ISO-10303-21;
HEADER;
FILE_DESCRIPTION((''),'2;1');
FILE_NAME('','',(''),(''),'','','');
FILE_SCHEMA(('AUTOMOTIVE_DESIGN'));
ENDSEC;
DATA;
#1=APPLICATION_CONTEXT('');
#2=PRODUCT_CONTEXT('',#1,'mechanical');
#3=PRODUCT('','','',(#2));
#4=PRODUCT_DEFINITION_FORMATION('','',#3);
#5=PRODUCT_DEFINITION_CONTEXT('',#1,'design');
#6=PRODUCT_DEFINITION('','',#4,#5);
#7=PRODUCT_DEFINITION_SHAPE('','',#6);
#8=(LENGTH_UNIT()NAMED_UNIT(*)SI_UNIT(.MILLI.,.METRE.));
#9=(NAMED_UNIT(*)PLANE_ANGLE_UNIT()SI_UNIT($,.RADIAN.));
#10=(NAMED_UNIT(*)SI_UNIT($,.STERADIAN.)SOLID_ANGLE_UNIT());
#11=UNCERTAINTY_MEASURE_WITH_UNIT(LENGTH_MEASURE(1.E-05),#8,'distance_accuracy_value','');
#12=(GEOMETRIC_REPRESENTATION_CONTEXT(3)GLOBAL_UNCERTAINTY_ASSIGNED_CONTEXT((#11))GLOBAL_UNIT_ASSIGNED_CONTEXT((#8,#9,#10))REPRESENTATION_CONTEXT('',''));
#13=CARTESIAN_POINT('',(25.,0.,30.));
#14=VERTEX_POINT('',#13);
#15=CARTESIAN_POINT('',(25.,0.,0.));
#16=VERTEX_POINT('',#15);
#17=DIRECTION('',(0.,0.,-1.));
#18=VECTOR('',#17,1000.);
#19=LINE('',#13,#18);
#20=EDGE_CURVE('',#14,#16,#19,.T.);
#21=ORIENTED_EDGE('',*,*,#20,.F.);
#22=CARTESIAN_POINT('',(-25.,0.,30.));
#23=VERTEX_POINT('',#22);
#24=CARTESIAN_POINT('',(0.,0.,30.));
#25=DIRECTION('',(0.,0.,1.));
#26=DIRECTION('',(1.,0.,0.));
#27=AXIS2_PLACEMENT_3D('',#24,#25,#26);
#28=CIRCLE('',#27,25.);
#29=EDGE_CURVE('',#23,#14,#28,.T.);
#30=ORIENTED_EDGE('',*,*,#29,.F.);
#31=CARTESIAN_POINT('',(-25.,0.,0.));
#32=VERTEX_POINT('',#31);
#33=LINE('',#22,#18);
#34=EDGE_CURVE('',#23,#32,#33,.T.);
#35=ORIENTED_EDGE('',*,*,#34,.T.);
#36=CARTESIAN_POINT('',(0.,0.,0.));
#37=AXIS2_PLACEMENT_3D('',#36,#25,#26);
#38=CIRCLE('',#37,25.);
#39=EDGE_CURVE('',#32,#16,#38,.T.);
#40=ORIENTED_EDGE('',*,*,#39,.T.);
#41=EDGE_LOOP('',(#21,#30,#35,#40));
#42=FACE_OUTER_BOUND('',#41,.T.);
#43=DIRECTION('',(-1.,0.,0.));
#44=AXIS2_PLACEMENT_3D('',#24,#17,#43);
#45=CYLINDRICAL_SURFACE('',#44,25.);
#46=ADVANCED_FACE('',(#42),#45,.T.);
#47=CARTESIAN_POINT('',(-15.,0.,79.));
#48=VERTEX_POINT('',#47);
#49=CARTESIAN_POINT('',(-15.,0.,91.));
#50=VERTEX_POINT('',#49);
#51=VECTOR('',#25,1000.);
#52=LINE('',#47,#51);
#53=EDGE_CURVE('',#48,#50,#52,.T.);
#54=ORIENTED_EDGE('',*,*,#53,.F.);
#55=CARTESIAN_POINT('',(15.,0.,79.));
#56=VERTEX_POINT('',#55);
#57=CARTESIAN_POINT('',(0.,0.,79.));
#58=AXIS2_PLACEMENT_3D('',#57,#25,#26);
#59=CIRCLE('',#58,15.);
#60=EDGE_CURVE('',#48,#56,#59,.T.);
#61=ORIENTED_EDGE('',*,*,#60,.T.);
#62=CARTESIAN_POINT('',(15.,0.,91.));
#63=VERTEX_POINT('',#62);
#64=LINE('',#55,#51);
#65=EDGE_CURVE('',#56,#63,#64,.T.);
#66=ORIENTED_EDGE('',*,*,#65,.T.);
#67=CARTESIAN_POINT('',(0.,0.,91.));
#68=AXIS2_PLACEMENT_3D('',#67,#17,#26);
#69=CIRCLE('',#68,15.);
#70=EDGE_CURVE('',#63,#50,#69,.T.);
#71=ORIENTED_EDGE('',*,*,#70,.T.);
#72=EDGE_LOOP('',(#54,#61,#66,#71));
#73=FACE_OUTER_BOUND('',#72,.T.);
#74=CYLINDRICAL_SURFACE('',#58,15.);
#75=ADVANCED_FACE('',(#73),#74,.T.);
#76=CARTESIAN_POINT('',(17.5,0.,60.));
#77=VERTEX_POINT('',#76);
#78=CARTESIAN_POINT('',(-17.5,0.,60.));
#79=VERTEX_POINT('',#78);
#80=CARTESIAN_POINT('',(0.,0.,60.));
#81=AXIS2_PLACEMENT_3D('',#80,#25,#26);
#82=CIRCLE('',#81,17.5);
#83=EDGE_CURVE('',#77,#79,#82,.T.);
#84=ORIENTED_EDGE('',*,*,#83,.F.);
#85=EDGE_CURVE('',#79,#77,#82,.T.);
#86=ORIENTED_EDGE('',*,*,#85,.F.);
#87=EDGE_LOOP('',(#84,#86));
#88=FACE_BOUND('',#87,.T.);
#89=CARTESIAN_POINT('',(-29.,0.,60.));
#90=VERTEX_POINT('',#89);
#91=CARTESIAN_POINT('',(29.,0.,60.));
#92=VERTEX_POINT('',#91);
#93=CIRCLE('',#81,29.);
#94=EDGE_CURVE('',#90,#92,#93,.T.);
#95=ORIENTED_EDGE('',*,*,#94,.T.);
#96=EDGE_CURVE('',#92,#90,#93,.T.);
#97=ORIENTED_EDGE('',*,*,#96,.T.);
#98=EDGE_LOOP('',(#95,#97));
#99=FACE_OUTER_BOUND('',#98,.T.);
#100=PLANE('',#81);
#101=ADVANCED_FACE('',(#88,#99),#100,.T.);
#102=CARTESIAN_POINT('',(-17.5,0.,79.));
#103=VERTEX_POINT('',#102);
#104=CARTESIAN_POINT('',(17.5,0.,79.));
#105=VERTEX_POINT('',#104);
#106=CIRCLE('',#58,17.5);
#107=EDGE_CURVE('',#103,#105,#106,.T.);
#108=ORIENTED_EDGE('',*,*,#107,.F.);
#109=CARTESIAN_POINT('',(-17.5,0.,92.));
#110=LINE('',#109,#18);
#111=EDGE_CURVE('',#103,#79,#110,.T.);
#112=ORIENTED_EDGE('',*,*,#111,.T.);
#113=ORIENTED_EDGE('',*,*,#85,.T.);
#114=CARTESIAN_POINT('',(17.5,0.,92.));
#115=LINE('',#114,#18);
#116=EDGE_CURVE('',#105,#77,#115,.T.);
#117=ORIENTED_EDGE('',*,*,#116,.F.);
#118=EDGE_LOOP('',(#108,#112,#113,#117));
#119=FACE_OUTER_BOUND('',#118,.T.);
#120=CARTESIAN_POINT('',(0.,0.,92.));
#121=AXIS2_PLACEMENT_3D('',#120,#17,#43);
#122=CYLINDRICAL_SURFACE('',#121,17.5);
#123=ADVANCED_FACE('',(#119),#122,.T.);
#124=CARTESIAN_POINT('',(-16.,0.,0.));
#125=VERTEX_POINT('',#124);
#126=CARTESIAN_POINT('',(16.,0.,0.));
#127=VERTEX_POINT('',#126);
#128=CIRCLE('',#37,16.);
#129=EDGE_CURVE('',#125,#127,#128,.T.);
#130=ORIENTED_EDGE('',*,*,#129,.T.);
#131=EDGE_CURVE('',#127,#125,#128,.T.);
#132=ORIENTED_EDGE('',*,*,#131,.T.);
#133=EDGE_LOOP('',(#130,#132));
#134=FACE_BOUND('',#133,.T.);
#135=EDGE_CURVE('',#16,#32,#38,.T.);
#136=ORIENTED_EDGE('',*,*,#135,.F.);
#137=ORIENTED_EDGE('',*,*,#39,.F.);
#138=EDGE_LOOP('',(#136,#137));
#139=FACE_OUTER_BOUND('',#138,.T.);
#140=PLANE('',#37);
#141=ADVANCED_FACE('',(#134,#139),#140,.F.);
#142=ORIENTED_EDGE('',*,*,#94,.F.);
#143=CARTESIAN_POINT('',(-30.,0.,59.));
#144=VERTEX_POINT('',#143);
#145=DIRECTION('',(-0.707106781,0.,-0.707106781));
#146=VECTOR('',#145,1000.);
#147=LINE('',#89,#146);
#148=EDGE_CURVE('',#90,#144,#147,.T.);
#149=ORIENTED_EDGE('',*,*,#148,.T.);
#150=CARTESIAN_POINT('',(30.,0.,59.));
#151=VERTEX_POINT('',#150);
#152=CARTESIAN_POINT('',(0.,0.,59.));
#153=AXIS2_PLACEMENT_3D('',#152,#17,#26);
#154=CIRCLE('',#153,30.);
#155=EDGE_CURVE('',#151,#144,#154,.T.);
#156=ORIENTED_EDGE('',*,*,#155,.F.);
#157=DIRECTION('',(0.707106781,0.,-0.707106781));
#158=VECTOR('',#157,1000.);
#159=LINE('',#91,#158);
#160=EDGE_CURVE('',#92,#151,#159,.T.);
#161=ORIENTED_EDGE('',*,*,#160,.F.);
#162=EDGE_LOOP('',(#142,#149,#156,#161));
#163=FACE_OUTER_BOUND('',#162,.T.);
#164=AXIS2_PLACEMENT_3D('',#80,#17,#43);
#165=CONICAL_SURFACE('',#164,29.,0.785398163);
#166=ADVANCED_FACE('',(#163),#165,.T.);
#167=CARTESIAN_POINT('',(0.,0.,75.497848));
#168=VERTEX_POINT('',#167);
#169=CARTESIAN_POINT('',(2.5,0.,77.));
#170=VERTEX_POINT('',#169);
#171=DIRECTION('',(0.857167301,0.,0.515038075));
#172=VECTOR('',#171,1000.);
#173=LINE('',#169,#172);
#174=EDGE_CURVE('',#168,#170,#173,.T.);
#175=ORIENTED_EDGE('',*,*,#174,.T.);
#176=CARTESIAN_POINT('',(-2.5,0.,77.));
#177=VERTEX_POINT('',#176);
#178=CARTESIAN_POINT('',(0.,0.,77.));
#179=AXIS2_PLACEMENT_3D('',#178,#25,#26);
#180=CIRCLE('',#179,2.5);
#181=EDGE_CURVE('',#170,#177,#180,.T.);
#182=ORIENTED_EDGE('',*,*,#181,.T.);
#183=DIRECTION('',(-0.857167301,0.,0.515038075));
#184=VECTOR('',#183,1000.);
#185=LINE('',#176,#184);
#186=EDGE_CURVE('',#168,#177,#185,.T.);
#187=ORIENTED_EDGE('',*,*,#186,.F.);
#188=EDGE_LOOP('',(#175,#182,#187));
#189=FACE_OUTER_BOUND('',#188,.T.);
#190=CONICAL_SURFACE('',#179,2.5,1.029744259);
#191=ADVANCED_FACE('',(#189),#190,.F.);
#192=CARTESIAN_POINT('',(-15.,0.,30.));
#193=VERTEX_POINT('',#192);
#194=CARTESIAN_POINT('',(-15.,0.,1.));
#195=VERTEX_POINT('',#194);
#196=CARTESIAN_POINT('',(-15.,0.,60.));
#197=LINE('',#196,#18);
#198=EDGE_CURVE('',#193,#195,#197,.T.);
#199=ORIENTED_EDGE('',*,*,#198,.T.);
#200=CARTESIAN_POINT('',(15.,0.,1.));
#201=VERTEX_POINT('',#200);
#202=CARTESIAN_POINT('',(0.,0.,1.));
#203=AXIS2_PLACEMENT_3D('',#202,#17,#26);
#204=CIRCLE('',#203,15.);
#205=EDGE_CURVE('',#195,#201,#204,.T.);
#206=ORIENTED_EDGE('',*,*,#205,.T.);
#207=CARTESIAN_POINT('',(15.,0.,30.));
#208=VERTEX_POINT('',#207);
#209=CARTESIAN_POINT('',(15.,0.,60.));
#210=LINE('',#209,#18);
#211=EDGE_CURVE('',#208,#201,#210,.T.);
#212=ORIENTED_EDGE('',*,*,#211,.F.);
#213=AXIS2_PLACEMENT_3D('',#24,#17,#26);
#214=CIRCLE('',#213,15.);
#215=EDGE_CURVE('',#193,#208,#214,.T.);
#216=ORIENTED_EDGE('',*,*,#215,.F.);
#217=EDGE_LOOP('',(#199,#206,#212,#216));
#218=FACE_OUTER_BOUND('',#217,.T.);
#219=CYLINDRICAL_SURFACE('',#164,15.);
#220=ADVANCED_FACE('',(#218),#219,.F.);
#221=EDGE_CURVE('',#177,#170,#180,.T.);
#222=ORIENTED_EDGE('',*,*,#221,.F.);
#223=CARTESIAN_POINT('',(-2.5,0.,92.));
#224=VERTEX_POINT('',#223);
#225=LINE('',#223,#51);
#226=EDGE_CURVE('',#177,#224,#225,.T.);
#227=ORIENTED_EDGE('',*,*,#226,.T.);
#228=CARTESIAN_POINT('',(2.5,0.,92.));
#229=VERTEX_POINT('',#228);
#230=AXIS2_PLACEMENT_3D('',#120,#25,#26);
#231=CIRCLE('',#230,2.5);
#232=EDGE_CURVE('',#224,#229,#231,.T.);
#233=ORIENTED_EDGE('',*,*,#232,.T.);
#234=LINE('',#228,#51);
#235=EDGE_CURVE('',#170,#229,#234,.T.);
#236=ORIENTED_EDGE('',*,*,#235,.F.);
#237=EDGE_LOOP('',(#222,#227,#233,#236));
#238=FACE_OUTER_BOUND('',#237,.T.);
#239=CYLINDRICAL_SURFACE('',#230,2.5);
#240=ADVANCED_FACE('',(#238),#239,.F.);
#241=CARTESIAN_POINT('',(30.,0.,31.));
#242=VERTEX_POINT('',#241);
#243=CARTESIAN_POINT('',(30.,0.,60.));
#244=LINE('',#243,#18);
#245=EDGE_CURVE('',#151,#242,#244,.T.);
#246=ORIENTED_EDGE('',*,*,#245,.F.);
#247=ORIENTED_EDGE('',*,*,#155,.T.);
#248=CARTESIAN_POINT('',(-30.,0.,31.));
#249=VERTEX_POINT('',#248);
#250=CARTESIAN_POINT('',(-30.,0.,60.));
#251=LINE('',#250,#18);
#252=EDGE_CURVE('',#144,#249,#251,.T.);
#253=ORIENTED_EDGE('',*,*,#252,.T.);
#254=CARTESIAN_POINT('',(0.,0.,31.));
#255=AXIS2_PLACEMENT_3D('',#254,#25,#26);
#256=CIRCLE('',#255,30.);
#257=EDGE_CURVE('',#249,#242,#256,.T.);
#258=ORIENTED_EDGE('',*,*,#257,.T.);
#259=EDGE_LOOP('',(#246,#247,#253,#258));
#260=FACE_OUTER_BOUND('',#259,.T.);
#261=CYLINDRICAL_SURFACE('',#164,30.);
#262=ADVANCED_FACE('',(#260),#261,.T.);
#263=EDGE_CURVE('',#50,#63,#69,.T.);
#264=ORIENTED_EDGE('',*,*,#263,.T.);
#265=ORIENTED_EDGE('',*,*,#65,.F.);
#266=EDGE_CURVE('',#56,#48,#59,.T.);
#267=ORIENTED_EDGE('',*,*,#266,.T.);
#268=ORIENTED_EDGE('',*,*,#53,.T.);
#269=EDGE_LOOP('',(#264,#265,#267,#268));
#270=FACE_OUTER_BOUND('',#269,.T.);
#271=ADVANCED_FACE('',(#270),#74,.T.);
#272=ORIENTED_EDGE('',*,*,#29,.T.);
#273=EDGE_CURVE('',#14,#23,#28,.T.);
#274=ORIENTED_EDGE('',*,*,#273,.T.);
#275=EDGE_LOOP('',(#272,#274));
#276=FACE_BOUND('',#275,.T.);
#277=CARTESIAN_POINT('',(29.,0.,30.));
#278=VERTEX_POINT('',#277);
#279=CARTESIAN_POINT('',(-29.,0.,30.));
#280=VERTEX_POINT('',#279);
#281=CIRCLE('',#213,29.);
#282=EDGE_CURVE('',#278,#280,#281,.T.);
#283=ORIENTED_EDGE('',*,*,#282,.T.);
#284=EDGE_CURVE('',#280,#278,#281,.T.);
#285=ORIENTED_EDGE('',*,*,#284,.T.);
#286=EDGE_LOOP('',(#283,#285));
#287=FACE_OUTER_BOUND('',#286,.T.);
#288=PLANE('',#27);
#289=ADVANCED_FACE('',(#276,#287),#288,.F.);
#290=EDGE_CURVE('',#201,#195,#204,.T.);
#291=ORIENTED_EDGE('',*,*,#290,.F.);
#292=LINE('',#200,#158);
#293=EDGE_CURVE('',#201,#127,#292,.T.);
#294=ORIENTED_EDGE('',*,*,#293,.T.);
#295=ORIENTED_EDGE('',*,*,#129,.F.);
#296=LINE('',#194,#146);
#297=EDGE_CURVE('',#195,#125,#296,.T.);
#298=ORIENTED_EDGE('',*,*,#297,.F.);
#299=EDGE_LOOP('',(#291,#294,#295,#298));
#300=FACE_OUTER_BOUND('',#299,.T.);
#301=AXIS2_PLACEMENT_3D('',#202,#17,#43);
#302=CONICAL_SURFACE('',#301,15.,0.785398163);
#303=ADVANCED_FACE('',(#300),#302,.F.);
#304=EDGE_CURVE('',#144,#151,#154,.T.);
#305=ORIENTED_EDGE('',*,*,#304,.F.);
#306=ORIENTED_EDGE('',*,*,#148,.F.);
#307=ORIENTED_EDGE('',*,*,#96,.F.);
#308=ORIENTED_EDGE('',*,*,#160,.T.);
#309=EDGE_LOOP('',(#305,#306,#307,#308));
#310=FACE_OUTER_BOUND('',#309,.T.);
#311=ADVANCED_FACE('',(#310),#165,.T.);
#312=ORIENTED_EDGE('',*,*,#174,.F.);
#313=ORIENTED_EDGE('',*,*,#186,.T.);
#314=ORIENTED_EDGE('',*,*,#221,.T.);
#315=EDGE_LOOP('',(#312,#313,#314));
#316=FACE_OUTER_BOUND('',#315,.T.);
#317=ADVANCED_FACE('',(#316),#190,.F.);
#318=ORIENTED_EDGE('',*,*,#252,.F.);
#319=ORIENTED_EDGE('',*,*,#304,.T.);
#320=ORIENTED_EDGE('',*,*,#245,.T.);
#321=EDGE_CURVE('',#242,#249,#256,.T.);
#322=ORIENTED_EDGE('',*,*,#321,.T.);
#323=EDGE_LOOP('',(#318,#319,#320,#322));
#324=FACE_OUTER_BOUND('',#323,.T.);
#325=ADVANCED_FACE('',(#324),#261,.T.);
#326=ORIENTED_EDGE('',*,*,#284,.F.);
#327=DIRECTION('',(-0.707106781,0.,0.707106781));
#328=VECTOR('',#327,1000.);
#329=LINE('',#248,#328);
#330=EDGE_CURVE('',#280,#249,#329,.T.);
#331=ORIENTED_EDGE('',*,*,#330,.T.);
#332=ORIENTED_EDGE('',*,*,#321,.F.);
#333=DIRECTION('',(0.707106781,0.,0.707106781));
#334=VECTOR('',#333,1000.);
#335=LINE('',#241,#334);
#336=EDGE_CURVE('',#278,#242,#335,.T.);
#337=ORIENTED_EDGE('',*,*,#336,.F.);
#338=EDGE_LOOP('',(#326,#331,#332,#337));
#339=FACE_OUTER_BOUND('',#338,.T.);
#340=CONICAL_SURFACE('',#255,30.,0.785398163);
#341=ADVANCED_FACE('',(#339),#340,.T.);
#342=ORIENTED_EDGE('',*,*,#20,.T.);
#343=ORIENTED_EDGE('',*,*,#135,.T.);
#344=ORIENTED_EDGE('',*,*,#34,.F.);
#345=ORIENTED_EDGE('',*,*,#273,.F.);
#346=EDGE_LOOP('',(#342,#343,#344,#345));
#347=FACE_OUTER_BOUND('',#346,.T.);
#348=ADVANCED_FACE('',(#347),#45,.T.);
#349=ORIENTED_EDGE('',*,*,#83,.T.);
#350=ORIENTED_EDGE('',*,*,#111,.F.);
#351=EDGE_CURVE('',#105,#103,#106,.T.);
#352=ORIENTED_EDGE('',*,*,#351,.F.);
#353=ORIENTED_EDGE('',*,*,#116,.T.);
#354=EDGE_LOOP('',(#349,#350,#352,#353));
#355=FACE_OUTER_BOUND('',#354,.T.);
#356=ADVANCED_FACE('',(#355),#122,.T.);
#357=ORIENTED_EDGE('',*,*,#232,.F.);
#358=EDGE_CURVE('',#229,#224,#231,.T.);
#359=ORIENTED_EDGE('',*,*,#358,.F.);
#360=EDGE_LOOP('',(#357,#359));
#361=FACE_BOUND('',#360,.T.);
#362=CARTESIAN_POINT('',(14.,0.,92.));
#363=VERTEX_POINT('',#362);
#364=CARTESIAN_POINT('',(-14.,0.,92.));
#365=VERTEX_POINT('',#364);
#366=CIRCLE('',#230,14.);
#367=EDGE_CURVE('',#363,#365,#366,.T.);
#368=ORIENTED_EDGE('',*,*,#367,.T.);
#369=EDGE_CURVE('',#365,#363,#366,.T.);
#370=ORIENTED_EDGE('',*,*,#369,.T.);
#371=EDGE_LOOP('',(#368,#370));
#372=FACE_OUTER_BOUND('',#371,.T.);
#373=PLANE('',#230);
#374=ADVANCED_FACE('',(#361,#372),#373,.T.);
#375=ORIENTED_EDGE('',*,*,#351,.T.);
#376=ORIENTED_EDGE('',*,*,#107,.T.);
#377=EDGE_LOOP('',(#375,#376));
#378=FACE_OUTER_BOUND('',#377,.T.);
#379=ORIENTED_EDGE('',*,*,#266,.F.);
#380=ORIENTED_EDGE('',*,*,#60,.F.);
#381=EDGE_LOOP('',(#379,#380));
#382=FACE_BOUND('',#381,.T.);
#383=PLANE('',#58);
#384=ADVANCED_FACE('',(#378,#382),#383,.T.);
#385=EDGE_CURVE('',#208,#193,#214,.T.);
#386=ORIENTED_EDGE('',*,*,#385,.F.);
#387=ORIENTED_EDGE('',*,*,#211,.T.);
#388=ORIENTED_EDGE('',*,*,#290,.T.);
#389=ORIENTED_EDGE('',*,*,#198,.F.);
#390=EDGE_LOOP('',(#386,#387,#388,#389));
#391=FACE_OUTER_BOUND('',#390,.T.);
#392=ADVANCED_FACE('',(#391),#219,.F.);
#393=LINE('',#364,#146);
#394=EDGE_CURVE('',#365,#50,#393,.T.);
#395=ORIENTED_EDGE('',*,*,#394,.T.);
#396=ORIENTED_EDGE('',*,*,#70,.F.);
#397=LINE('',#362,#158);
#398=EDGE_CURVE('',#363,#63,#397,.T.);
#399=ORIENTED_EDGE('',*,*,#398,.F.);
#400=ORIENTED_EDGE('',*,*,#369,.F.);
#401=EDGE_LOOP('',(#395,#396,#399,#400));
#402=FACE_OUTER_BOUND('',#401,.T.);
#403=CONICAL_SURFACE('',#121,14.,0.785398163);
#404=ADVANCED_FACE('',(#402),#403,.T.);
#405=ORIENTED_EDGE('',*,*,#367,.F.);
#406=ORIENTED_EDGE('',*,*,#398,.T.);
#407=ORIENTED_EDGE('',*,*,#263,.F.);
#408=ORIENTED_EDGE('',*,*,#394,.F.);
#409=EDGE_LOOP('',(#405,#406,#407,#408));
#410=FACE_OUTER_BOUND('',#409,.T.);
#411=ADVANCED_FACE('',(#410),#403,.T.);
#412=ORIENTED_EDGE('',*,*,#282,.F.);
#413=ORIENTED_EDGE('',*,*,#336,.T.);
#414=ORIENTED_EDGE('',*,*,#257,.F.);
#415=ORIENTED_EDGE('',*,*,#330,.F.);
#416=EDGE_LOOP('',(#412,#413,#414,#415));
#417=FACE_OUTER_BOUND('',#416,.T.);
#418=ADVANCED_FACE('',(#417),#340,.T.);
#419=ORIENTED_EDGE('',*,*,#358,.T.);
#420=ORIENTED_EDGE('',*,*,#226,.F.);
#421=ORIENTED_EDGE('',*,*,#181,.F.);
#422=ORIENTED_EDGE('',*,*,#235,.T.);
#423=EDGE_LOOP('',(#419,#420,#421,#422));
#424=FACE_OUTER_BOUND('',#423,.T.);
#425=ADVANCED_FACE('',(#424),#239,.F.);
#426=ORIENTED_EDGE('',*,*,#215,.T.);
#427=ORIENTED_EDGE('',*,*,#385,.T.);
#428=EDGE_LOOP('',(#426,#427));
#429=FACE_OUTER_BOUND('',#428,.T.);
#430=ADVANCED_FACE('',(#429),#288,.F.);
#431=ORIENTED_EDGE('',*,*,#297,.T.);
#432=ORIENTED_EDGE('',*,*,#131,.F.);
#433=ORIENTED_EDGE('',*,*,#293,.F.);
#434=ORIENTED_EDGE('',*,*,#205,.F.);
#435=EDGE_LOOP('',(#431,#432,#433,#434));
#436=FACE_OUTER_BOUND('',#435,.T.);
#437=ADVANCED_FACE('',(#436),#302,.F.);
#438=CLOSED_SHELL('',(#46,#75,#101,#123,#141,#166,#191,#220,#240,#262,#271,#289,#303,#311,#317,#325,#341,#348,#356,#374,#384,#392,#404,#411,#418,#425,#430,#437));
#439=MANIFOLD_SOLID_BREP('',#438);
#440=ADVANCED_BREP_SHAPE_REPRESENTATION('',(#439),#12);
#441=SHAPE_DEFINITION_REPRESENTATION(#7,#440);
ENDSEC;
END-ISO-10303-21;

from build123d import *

# Parameters (mm, degrees)
SKETCH_1_R             = 25
EXTRUDE_1_DEPTH        = 30
SKETCH_2_R             = 30
EXTRUDE_2_DEPTH        = 30
SKETCH_4_R             = 15
CUT_EXTRUDE_1_DEPTH    = 74.484692283
EXTRUDE_START          = -30
SKETCH_13_R            = 15
EXTRUDE_4_DEPTH        = 30
SKETCH_12_R            = 17.5
EXTRUDE_3_DEPTH        = 32
HOLE_WIZARD_M6_1_D     = 5
HOLE_WIZARD_M6_1_DEPTH = 15
HOLE_WIZARD_M6_1_TIP   = 1.502151548
CUT_EXTRUDE_START      = -13
SKETCH_16_R            = 17.5
SKETCH_16_R_2          = 15
CUT_EXTRUDE_3_DEPTH    = 13
CHAMFER_4_SIZE         = 1


with BuildPart() as part:
    # 草图1 → 凸台-拉伸1 (new body)
    with BuildSketch(Plane.XY):
        Circle(SKETCH_1_R)
    extrude(amount=EXTRUDE_1_DEPTH)

    # 草图2 → 凸台-拉伸2 (add)
    with BuildSketch(Plane.XY.offset(30)):
        Circle(SKETCH_2_R)
    extrude(amount=EXTRUDE_2_DEPTH)

    # 草图4 → 切除-拉伸1 (cut, through all)
    with BuildSketch(Plane(origin=(0, 0, 0), x_dir=(-1, 0, 0), z_dir=(0, 0, -1))):
        Circle(SKETCH_4_R)
    extrude(amount=-CUT_EXTRUDE_1_DEPTH, mode=Mode.SUBTRACT)

    # 草图13 → 凸台-拉伸4 (add)
    with BuildSketch(Plane.XY.offset(60).offset(EXTRUDE_START)):
        with Locations(Location((0, 0, 0), (0, 0, 180))):
            Circle(SKETCH_13_R)
    extrude(amount=EXTRUDE_4_DEPTH)

    # 草图12 → 凸台-拉伸3 (add)
    with BuildSketch(Plane.XY.offset(60)):
        Circle(SKETCH_12_R)
    extrude(amount=EXTRUDE_3_DEPTH)

    # M6 螺纹孔1
    with Locations(Plane.XY.offset(92)):
        with Locations((0, 0)):
            Hole(HOLE_WIZARD_M6_1_D / 2, depth=HOLE_WIZARD_M6_1_DEPTH)
            with Locations((0, 0, -(HOLE_WIZARD_M6_1_DEPTH + HOLE_WIZARD_M6_1_TIP / 2))):  # 118° drill point
                Cone(0, HOLE_WIZARD_M6_1_D / 2, HOLE_WIZARD_M6_1_TIP, mode=Mode.SUBTRACT)

    # 草图16 → 切除-拉伸3 (cut)
    with BuildSketch(Plane.XY.offset(92).offset(CUT_EXTRUDE_START)):
        Circle(SKETCH_16_R)
        with Locations(Location((0, 0, 0), (0, 0, 180))):
            Circle(SKETCH_16_R_2, mode=Mode.SUBTRACT)
    extrude(amount=CUT_EXTRUDE_3_DEPTH, mode=Mode.SUBTRACT)

    # 倒角4
    chamfer_4_edges = [part.edges().sort_by_distance(p)[0] for p in [
        (15, 0, 0),
        (15, 0, 92),
        (-30, 0, 30),
        (-30, 0, 60),
    ]]
    chamfer(chamfer_4_edges, length=CHAMFER_4_SIZE)


solid = part.part
